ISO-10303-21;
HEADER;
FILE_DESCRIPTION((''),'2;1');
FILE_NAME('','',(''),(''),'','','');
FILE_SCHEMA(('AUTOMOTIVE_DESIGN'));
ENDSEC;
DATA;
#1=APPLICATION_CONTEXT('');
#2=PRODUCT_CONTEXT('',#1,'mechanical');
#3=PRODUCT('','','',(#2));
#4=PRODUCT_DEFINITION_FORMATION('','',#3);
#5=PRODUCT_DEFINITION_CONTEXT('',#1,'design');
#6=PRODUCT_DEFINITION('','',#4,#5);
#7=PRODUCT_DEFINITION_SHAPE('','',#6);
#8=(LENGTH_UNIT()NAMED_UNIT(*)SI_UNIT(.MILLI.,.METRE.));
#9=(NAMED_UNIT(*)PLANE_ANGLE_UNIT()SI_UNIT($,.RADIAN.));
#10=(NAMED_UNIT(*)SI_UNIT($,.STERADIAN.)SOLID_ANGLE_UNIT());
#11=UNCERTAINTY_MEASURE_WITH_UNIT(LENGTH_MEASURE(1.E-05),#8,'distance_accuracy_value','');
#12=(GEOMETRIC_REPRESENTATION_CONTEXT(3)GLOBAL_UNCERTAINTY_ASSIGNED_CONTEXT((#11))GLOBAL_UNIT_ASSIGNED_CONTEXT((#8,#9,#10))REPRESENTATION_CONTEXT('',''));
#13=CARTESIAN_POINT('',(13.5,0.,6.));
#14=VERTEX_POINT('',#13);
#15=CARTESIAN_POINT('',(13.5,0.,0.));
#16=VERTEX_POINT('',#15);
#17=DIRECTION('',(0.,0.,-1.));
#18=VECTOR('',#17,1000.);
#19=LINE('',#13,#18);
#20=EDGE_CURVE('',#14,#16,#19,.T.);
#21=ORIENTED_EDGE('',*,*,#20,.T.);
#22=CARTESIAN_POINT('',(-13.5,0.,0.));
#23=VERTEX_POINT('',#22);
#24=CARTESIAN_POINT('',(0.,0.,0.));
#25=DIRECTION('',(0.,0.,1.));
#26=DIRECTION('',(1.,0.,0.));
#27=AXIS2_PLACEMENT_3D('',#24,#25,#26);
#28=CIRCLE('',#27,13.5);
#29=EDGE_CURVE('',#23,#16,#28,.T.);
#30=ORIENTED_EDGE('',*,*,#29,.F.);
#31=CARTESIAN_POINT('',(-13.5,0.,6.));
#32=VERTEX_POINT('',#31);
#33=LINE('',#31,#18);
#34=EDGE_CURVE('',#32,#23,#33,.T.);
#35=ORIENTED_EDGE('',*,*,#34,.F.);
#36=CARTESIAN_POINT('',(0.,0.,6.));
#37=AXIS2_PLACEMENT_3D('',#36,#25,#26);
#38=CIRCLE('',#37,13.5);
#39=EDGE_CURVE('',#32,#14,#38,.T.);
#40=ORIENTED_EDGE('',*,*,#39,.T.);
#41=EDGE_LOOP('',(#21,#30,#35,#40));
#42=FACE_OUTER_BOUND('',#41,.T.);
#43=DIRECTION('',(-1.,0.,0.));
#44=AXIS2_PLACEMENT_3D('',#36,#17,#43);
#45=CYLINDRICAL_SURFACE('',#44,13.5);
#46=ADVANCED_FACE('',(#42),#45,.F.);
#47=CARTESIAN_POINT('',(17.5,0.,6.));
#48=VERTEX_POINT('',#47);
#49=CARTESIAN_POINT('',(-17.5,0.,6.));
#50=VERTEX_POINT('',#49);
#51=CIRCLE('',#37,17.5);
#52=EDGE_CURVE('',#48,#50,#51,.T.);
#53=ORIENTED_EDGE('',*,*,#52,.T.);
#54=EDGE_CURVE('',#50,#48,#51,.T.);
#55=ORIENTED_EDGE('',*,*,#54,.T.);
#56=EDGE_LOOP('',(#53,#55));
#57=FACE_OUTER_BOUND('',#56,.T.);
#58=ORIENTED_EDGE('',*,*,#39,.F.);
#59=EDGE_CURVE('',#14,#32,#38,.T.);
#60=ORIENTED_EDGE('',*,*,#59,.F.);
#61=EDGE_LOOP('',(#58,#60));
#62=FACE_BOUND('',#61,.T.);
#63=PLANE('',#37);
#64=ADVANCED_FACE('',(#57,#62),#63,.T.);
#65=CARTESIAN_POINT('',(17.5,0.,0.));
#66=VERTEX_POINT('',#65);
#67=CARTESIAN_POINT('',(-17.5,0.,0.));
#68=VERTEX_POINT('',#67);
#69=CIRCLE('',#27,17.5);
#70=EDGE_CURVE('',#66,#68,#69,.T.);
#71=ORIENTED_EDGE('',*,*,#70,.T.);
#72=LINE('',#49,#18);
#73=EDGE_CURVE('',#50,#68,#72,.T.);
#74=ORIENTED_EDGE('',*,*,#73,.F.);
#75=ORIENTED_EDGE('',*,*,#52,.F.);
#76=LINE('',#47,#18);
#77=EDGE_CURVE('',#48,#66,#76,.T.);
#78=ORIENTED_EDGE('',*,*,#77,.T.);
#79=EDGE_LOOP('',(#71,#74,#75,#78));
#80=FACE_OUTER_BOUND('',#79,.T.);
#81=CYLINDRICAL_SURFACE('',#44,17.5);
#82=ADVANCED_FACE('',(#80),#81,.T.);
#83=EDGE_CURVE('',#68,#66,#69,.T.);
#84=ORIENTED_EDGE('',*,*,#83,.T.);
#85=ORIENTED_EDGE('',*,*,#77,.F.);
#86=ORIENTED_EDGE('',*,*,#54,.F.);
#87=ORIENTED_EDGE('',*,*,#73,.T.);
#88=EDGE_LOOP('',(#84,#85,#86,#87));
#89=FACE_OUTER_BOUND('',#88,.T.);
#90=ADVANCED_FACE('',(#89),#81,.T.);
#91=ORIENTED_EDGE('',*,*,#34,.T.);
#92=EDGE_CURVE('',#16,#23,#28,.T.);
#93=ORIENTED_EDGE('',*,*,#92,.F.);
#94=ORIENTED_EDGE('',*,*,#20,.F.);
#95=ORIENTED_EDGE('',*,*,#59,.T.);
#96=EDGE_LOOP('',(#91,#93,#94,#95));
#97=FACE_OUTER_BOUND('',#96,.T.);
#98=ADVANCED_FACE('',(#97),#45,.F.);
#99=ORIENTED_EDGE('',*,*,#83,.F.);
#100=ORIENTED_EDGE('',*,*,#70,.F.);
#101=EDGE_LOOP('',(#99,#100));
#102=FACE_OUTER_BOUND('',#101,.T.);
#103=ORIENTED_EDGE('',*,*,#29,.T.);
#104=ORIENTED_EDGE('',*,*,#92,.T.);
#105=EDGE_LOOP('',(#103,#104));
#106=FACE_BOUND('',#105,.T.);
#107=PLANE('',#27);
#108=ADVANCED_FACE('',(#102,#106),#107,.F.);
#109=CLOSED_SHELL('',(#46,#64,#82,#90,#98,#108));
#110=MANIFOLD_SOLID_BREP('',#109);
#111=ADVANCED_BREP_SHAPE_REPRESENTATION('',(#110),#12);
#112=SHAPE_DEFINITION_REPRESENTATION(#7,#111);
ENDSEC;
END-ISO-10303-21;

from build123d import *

# Parameters (mm, degrees)
SKETCH1_R           = 17.5
SKETCH1_R_2         = 13.5
BOSS_EXTRUDE1_DEPTH = 6


with BuildPart() as part:
    # Sketch1 → Boss-Extrude1 (new body)
    with BuildSketch(Plane.XY):
        Circle(SKETCH1_R)
        Circle(SKETCH1_R_2, mode=Mode.SUBTRACT)
    extrude(amount=BOSS_EXTRUDE1_DEPTH)


solid = part.part
